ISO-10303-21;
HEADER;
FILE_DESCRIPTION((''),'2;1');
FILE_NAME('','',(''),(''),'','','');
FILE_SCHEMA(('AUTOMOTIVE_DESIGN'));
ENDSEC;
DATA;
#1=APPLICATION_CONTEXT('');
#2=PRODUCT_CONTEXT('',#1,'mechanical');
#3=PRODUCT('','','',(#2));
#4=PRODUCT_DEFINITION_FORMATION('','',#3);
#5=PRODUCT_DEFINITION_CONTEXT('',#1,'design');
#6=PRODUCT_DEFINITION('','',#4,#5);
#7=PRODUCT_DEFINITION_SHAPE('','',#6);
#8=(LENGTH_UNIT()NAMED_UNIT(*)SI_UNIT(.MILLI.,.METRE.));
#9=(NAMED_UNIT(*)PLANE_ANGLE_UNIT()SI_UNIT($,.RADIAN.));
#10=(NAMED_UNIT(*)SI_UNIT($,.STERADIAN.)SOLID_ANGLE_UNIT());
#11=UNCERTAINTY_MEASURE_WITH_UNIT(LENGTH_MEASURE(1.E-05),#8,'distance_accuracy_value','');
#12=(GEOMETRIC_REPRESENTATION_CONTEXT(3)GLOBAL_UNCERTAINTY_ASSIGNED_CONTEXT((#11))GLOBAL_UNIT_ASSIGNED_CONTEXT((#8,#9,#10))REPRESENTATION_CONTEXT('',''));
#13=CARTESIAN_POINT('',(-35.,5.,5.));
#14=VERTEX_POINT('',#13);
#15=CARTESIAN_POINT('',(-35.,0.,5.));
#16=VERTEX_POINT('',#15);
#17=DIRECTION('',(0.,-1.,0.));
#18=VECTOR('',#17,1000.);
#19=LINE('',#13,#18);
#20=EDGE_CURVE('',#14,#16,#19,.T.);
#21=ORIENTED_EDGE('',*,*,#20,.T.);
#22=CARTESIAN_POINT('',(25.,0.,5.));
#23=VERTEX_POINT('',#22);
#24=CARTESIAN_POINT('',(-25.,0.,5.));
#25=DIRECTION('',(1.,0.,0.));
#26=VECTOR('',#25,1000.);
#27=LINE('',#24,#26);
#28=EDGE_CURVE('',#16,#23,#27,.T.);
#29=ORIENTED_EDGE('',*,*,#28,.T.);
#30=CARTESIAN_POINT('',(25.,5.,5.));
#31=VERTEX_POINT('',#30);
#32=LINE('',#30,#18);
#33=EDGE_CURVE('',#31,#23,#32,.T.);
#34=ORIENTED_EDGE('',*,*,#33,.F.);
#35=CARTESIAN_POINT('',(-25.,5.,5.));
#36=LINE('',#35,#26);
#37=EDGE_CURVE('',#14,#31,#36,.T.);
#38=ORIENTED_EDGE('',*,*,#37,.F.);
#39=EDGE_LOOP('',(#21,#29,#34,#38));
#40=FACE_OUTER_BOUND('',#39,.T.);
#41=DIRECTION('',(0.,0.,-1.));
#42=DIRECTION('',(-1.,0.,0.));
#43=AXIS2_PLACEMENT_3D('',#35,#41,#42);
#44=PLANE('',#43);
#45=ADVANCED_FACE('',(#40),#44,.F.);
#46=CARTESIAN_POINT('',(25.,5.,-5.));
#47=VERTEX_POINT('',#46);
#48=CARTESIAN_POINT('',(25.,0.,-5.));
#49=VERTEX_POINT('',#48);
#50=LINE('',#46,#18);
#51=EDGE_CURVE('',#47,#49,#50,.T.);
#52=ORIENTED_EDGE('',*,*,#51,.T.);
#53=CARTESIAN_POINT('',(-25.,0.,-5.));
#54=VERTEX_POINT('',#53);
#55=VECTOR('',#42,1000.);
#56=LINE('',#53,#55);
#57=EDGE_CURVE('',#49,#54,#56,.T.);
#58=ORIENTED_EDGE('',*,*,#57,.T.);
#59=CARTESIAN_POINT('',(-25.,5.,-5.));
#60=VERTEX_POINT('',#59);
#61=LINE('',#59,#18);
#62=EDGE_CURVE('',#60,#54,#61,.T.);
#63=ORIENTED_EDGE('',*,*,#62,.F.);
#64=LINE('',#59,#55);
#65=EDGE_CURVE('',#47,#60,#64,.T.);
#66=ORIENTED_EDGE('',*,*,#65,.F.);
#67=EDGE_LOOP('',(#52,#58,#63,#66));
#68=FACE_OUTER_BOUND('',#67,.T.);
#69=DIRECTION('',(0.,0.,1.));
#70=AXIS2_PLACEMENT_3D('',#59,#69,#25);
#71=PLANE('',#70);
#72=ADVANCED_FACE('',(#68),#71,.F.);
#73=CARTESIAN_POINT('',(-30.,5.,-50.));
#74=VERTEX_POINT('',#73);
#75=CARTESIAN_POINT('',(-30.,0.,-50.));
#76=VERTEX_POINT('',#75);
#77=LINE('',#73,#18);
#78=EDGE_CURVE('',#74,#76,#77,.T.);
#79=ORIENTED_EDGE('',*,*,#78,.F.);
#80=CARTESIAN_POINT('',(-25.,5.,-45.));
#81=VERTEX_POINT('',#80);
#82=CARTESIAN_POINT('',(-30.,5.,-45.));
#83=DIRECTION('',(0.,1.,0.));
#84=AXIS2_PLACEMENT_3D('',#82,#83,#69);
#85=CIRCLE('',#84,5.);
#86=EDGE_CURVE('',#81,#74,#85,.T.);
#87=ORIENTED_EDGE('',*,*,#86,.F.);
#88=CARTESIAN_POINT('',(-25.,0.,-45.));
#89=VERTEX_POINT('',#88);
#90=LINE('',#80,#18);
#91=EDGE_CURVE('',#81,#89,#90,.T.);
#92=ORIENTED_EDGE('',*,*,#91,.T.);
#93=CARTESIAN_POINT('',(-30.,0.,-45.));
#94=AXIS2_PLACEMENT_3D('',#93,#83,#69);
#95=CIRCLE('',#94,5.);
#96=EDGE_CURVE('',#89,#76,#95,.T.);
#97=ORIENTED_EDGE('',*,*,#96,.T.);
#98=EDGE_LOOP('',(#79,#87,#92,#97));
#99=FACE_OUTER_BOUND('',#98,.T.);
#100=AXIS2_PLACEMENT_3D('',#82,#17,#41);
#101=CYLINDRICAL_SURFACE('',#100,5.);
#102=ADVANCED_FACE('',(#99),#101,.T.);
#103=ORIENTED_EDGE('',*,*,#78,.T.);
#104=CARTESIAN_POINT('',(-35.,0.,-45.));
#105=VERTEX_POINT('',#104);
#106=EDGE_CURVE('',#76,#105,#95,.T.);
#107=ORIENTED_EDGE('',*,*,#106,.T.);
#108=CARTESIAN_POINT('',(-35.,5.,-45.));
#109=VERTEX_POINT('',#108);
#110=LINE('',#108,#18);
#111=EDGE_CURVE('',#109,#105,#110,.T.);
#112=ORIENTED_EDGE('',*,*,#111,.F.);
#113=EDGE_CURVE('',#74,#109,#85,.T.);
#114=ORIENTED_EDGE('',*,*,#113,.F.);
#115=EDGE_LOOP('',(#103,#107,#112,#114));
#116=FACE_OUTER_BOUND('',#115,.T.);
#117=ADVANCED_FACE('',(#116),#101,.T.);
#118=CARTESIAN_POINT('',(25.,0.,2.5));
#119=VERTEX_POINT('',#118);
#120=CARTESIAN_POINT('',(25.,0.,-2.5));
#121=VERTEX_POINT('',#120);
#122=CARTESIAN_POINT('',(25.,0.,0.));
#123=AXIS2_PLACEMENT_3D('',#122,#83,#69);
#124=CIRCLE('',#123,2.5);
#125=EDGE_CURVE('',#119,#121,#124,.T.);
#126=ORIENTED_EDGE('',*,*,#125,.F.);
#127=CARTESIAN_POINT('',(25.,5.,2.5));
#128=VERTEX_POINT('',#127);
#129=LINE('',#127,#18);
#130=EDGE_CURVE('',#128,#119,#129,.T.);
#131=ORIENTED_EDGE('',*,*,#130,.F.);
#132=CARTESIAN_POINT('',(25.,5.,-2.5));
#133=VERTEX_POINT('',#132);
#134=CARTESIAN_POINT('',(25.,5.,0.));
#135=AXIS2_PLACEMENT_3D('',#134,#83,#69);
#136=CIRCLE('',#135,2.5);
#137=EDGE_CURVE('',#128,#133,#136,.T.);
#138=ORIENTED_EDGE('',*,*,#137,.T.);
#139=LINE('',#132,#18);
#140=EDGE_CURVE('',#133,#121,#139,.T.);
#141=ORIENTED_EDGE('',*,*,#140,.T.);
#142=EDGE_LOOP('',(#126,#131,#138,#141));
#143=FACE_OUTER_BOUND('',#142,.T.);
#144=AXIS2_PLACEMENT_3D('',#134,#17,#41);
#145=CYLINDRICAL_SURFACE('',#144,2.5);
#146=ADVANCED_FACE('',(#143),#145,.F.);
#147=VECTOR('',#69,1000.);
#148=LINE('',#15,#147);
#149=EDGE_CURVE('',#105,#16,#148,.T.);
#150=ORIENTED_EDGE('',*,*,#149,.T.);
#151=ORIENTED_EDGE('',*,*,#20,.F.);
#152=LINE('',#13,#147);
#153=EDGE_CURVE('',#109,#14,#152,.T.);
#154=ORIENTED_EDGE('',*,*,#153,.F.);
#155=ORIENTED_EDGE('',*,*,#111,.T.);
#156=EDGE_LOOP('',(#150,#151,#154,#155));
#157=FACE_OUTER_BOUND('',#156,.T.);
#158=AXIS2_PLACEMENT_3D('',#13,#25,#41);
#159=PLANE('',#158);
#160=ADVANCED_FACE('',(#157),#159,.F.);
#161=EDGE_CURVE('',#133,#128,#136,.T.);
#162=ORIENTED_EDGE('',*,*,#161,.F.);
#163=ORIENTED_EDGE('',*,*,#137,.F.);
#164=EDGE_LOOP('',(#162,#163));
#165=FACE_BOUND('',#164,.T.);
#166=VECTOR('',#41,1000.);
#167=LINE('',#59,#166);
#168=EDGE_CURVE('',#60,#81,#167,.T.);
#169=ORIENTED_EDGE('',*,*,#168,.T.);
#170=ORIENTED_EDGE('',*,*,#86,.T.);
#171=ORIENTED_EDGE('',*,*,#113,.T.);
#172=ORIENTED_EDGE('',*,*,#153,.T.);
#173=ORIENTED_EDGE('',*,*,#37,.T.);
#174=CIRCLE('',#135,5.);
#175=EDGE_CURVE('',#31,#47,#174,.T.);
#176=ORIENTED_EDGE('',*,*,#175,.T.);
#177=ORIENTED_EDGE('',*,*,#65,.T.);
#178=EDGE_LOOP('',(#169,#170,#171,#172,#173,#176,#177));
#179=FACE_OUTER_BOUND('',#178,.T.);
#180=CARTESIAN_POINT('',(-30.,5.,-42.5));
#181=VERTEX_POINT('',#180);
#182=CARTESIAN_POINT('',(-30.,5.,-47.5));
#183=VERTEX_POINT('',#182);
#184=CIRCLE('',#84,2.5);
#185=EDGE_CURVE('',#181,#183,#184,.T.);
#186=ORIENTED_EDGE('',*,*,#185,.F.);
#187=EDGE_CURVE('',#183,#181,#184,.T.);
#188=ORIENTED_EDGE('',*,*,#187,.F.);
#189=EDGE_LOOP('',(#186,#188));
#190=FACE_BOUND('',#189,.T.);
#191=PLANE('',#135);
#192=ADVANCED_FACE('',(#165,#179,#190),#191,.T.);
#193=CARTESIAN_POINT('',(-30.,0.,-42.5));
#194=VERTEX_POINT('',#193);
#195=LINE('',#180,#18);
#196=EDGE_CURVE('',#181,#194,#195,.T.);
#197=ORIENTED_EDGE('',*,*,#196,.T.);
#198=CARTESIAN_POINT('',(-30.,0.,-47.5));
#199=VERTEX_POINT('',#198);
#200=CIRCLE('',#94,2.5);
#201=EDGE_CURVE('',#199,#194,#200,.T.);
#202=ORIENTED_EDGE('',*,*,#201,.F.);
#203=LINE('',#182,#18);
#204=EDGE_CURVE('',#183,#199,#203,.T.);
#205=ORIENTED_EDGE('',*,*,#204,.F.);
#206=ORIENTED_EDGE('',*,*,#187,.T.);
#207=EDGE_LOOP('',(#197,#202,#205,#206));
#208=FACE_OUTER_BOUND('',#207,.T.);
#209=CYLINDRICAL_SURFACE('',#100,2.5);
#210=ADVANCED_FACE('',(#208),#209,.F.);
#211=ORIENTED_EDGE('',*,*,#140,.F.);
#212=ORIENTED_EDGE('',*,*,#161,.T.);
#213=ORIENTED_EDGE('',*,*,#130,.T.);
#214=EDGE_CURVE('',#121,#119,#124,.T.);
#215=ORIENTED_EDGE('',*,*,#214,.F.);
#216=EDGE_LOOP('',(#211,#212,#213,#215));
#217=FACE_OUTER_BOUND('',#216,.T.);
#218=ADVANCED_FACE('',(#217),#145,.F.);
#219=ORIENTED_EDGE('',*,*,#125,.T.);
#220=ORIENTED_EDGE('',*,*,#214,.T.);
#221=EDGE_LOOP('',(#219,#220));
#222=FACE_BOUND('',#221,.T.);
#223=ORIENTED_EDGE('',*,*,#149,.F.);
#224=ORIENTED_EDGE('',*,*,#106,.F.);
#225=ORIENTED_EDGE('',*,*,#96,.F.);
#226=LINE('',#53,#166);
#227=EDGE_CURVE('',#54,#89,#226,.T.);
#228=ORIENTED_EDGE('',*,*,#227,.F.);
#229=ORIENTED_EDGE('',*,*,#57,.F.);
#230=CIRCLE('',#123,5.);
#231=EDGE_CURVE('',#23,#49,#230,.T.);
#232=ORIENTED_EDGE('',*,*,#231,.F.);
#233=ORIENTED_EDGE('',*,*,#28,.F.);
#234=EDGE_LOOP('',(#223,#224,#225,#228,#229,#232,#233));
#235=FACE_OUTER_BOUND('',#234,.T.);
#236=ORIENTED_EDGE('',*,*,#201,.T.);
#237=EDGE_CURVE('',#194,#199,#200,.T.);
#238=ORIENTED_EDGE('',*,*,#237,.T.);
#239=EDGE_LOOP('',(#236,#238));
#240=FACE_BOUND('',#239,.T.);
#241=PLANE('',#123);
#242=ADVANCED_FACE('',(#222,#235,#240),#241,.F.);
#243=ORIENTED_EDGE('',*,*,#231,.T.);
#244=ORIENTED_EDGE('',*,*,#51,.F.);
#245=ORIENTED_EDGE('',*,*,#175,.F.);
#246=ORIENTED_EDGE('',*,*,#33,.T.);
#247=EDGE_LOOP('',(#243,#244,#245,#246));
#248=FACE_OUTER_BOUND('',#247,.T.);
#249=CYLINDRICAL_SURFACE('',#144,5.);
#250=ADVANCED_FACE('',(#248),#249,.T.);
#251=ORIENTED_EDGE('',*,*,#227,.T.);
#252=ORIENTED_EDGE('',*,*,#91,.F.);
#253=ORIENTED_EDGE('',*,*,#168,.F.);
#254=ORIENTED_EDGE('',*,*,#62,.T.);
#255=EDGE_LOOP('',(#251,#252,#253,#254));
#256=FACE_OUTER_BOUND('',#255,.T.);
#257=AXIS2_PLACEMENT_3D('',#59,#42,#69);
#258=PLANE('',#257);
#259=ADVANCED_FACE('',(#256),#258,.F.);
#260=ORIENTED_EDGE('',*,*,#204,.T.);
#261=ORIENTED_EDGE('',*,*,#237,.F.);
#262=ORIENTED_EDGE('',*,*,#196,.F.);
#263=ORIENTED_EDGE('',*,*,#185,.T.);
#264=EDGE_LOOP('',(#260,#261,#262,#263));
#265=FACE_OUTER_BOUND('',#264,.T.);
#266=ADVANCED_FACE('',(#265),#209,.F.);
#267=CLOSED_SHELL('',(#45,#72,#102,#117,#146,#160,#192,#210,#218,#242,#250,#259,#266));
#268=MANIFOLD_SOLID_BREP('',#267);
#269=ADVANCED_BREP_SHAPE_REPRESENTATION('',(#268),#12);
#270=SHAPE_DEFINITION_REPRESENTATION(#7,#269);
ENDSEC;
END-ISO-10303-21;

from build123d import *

# Parameters (mm, degrees)
SKETCH1_R           = 2.5
BOSS_EXTRUDE1_DEPTH = 5


with BuildPart() as part:
    # Sketch1 → Boss-Extrude1 (new body)
    with BuildSketch(Plane(origin=(0, 0, 0), x_dir=(1, 0, 0), z_dir=(0, 1, 0))):
        with BuildLine():
            Line((-25, -5), (25, -5))
            ThreePointArc((25, -5), (30, 0), (25, 5))
            Line((25, 5), (-25, 5))
            Line((-25, 5), (-25, 45))
            ThreePointArc((-25, 45), (-30, 50), (-35, 45))
            Line((-35, 45), (-35, -5))
            Line((-35, -5), (-25, -5))
        make_face()
        with Locations(Location((25, 0, 0), (0, 0, 270))):
            Circle(SKETCH1_R, mode=Mode.SUBTRACT)
        with Locations(Location((-30, 45, 0), (0, 0, 270))):
            Circle(SKETCH1_R, mode=Mode.SUBTRACT)
    extrude(amount=BOSS_EXTRUDE1_DEPTH)


solid = part.part
